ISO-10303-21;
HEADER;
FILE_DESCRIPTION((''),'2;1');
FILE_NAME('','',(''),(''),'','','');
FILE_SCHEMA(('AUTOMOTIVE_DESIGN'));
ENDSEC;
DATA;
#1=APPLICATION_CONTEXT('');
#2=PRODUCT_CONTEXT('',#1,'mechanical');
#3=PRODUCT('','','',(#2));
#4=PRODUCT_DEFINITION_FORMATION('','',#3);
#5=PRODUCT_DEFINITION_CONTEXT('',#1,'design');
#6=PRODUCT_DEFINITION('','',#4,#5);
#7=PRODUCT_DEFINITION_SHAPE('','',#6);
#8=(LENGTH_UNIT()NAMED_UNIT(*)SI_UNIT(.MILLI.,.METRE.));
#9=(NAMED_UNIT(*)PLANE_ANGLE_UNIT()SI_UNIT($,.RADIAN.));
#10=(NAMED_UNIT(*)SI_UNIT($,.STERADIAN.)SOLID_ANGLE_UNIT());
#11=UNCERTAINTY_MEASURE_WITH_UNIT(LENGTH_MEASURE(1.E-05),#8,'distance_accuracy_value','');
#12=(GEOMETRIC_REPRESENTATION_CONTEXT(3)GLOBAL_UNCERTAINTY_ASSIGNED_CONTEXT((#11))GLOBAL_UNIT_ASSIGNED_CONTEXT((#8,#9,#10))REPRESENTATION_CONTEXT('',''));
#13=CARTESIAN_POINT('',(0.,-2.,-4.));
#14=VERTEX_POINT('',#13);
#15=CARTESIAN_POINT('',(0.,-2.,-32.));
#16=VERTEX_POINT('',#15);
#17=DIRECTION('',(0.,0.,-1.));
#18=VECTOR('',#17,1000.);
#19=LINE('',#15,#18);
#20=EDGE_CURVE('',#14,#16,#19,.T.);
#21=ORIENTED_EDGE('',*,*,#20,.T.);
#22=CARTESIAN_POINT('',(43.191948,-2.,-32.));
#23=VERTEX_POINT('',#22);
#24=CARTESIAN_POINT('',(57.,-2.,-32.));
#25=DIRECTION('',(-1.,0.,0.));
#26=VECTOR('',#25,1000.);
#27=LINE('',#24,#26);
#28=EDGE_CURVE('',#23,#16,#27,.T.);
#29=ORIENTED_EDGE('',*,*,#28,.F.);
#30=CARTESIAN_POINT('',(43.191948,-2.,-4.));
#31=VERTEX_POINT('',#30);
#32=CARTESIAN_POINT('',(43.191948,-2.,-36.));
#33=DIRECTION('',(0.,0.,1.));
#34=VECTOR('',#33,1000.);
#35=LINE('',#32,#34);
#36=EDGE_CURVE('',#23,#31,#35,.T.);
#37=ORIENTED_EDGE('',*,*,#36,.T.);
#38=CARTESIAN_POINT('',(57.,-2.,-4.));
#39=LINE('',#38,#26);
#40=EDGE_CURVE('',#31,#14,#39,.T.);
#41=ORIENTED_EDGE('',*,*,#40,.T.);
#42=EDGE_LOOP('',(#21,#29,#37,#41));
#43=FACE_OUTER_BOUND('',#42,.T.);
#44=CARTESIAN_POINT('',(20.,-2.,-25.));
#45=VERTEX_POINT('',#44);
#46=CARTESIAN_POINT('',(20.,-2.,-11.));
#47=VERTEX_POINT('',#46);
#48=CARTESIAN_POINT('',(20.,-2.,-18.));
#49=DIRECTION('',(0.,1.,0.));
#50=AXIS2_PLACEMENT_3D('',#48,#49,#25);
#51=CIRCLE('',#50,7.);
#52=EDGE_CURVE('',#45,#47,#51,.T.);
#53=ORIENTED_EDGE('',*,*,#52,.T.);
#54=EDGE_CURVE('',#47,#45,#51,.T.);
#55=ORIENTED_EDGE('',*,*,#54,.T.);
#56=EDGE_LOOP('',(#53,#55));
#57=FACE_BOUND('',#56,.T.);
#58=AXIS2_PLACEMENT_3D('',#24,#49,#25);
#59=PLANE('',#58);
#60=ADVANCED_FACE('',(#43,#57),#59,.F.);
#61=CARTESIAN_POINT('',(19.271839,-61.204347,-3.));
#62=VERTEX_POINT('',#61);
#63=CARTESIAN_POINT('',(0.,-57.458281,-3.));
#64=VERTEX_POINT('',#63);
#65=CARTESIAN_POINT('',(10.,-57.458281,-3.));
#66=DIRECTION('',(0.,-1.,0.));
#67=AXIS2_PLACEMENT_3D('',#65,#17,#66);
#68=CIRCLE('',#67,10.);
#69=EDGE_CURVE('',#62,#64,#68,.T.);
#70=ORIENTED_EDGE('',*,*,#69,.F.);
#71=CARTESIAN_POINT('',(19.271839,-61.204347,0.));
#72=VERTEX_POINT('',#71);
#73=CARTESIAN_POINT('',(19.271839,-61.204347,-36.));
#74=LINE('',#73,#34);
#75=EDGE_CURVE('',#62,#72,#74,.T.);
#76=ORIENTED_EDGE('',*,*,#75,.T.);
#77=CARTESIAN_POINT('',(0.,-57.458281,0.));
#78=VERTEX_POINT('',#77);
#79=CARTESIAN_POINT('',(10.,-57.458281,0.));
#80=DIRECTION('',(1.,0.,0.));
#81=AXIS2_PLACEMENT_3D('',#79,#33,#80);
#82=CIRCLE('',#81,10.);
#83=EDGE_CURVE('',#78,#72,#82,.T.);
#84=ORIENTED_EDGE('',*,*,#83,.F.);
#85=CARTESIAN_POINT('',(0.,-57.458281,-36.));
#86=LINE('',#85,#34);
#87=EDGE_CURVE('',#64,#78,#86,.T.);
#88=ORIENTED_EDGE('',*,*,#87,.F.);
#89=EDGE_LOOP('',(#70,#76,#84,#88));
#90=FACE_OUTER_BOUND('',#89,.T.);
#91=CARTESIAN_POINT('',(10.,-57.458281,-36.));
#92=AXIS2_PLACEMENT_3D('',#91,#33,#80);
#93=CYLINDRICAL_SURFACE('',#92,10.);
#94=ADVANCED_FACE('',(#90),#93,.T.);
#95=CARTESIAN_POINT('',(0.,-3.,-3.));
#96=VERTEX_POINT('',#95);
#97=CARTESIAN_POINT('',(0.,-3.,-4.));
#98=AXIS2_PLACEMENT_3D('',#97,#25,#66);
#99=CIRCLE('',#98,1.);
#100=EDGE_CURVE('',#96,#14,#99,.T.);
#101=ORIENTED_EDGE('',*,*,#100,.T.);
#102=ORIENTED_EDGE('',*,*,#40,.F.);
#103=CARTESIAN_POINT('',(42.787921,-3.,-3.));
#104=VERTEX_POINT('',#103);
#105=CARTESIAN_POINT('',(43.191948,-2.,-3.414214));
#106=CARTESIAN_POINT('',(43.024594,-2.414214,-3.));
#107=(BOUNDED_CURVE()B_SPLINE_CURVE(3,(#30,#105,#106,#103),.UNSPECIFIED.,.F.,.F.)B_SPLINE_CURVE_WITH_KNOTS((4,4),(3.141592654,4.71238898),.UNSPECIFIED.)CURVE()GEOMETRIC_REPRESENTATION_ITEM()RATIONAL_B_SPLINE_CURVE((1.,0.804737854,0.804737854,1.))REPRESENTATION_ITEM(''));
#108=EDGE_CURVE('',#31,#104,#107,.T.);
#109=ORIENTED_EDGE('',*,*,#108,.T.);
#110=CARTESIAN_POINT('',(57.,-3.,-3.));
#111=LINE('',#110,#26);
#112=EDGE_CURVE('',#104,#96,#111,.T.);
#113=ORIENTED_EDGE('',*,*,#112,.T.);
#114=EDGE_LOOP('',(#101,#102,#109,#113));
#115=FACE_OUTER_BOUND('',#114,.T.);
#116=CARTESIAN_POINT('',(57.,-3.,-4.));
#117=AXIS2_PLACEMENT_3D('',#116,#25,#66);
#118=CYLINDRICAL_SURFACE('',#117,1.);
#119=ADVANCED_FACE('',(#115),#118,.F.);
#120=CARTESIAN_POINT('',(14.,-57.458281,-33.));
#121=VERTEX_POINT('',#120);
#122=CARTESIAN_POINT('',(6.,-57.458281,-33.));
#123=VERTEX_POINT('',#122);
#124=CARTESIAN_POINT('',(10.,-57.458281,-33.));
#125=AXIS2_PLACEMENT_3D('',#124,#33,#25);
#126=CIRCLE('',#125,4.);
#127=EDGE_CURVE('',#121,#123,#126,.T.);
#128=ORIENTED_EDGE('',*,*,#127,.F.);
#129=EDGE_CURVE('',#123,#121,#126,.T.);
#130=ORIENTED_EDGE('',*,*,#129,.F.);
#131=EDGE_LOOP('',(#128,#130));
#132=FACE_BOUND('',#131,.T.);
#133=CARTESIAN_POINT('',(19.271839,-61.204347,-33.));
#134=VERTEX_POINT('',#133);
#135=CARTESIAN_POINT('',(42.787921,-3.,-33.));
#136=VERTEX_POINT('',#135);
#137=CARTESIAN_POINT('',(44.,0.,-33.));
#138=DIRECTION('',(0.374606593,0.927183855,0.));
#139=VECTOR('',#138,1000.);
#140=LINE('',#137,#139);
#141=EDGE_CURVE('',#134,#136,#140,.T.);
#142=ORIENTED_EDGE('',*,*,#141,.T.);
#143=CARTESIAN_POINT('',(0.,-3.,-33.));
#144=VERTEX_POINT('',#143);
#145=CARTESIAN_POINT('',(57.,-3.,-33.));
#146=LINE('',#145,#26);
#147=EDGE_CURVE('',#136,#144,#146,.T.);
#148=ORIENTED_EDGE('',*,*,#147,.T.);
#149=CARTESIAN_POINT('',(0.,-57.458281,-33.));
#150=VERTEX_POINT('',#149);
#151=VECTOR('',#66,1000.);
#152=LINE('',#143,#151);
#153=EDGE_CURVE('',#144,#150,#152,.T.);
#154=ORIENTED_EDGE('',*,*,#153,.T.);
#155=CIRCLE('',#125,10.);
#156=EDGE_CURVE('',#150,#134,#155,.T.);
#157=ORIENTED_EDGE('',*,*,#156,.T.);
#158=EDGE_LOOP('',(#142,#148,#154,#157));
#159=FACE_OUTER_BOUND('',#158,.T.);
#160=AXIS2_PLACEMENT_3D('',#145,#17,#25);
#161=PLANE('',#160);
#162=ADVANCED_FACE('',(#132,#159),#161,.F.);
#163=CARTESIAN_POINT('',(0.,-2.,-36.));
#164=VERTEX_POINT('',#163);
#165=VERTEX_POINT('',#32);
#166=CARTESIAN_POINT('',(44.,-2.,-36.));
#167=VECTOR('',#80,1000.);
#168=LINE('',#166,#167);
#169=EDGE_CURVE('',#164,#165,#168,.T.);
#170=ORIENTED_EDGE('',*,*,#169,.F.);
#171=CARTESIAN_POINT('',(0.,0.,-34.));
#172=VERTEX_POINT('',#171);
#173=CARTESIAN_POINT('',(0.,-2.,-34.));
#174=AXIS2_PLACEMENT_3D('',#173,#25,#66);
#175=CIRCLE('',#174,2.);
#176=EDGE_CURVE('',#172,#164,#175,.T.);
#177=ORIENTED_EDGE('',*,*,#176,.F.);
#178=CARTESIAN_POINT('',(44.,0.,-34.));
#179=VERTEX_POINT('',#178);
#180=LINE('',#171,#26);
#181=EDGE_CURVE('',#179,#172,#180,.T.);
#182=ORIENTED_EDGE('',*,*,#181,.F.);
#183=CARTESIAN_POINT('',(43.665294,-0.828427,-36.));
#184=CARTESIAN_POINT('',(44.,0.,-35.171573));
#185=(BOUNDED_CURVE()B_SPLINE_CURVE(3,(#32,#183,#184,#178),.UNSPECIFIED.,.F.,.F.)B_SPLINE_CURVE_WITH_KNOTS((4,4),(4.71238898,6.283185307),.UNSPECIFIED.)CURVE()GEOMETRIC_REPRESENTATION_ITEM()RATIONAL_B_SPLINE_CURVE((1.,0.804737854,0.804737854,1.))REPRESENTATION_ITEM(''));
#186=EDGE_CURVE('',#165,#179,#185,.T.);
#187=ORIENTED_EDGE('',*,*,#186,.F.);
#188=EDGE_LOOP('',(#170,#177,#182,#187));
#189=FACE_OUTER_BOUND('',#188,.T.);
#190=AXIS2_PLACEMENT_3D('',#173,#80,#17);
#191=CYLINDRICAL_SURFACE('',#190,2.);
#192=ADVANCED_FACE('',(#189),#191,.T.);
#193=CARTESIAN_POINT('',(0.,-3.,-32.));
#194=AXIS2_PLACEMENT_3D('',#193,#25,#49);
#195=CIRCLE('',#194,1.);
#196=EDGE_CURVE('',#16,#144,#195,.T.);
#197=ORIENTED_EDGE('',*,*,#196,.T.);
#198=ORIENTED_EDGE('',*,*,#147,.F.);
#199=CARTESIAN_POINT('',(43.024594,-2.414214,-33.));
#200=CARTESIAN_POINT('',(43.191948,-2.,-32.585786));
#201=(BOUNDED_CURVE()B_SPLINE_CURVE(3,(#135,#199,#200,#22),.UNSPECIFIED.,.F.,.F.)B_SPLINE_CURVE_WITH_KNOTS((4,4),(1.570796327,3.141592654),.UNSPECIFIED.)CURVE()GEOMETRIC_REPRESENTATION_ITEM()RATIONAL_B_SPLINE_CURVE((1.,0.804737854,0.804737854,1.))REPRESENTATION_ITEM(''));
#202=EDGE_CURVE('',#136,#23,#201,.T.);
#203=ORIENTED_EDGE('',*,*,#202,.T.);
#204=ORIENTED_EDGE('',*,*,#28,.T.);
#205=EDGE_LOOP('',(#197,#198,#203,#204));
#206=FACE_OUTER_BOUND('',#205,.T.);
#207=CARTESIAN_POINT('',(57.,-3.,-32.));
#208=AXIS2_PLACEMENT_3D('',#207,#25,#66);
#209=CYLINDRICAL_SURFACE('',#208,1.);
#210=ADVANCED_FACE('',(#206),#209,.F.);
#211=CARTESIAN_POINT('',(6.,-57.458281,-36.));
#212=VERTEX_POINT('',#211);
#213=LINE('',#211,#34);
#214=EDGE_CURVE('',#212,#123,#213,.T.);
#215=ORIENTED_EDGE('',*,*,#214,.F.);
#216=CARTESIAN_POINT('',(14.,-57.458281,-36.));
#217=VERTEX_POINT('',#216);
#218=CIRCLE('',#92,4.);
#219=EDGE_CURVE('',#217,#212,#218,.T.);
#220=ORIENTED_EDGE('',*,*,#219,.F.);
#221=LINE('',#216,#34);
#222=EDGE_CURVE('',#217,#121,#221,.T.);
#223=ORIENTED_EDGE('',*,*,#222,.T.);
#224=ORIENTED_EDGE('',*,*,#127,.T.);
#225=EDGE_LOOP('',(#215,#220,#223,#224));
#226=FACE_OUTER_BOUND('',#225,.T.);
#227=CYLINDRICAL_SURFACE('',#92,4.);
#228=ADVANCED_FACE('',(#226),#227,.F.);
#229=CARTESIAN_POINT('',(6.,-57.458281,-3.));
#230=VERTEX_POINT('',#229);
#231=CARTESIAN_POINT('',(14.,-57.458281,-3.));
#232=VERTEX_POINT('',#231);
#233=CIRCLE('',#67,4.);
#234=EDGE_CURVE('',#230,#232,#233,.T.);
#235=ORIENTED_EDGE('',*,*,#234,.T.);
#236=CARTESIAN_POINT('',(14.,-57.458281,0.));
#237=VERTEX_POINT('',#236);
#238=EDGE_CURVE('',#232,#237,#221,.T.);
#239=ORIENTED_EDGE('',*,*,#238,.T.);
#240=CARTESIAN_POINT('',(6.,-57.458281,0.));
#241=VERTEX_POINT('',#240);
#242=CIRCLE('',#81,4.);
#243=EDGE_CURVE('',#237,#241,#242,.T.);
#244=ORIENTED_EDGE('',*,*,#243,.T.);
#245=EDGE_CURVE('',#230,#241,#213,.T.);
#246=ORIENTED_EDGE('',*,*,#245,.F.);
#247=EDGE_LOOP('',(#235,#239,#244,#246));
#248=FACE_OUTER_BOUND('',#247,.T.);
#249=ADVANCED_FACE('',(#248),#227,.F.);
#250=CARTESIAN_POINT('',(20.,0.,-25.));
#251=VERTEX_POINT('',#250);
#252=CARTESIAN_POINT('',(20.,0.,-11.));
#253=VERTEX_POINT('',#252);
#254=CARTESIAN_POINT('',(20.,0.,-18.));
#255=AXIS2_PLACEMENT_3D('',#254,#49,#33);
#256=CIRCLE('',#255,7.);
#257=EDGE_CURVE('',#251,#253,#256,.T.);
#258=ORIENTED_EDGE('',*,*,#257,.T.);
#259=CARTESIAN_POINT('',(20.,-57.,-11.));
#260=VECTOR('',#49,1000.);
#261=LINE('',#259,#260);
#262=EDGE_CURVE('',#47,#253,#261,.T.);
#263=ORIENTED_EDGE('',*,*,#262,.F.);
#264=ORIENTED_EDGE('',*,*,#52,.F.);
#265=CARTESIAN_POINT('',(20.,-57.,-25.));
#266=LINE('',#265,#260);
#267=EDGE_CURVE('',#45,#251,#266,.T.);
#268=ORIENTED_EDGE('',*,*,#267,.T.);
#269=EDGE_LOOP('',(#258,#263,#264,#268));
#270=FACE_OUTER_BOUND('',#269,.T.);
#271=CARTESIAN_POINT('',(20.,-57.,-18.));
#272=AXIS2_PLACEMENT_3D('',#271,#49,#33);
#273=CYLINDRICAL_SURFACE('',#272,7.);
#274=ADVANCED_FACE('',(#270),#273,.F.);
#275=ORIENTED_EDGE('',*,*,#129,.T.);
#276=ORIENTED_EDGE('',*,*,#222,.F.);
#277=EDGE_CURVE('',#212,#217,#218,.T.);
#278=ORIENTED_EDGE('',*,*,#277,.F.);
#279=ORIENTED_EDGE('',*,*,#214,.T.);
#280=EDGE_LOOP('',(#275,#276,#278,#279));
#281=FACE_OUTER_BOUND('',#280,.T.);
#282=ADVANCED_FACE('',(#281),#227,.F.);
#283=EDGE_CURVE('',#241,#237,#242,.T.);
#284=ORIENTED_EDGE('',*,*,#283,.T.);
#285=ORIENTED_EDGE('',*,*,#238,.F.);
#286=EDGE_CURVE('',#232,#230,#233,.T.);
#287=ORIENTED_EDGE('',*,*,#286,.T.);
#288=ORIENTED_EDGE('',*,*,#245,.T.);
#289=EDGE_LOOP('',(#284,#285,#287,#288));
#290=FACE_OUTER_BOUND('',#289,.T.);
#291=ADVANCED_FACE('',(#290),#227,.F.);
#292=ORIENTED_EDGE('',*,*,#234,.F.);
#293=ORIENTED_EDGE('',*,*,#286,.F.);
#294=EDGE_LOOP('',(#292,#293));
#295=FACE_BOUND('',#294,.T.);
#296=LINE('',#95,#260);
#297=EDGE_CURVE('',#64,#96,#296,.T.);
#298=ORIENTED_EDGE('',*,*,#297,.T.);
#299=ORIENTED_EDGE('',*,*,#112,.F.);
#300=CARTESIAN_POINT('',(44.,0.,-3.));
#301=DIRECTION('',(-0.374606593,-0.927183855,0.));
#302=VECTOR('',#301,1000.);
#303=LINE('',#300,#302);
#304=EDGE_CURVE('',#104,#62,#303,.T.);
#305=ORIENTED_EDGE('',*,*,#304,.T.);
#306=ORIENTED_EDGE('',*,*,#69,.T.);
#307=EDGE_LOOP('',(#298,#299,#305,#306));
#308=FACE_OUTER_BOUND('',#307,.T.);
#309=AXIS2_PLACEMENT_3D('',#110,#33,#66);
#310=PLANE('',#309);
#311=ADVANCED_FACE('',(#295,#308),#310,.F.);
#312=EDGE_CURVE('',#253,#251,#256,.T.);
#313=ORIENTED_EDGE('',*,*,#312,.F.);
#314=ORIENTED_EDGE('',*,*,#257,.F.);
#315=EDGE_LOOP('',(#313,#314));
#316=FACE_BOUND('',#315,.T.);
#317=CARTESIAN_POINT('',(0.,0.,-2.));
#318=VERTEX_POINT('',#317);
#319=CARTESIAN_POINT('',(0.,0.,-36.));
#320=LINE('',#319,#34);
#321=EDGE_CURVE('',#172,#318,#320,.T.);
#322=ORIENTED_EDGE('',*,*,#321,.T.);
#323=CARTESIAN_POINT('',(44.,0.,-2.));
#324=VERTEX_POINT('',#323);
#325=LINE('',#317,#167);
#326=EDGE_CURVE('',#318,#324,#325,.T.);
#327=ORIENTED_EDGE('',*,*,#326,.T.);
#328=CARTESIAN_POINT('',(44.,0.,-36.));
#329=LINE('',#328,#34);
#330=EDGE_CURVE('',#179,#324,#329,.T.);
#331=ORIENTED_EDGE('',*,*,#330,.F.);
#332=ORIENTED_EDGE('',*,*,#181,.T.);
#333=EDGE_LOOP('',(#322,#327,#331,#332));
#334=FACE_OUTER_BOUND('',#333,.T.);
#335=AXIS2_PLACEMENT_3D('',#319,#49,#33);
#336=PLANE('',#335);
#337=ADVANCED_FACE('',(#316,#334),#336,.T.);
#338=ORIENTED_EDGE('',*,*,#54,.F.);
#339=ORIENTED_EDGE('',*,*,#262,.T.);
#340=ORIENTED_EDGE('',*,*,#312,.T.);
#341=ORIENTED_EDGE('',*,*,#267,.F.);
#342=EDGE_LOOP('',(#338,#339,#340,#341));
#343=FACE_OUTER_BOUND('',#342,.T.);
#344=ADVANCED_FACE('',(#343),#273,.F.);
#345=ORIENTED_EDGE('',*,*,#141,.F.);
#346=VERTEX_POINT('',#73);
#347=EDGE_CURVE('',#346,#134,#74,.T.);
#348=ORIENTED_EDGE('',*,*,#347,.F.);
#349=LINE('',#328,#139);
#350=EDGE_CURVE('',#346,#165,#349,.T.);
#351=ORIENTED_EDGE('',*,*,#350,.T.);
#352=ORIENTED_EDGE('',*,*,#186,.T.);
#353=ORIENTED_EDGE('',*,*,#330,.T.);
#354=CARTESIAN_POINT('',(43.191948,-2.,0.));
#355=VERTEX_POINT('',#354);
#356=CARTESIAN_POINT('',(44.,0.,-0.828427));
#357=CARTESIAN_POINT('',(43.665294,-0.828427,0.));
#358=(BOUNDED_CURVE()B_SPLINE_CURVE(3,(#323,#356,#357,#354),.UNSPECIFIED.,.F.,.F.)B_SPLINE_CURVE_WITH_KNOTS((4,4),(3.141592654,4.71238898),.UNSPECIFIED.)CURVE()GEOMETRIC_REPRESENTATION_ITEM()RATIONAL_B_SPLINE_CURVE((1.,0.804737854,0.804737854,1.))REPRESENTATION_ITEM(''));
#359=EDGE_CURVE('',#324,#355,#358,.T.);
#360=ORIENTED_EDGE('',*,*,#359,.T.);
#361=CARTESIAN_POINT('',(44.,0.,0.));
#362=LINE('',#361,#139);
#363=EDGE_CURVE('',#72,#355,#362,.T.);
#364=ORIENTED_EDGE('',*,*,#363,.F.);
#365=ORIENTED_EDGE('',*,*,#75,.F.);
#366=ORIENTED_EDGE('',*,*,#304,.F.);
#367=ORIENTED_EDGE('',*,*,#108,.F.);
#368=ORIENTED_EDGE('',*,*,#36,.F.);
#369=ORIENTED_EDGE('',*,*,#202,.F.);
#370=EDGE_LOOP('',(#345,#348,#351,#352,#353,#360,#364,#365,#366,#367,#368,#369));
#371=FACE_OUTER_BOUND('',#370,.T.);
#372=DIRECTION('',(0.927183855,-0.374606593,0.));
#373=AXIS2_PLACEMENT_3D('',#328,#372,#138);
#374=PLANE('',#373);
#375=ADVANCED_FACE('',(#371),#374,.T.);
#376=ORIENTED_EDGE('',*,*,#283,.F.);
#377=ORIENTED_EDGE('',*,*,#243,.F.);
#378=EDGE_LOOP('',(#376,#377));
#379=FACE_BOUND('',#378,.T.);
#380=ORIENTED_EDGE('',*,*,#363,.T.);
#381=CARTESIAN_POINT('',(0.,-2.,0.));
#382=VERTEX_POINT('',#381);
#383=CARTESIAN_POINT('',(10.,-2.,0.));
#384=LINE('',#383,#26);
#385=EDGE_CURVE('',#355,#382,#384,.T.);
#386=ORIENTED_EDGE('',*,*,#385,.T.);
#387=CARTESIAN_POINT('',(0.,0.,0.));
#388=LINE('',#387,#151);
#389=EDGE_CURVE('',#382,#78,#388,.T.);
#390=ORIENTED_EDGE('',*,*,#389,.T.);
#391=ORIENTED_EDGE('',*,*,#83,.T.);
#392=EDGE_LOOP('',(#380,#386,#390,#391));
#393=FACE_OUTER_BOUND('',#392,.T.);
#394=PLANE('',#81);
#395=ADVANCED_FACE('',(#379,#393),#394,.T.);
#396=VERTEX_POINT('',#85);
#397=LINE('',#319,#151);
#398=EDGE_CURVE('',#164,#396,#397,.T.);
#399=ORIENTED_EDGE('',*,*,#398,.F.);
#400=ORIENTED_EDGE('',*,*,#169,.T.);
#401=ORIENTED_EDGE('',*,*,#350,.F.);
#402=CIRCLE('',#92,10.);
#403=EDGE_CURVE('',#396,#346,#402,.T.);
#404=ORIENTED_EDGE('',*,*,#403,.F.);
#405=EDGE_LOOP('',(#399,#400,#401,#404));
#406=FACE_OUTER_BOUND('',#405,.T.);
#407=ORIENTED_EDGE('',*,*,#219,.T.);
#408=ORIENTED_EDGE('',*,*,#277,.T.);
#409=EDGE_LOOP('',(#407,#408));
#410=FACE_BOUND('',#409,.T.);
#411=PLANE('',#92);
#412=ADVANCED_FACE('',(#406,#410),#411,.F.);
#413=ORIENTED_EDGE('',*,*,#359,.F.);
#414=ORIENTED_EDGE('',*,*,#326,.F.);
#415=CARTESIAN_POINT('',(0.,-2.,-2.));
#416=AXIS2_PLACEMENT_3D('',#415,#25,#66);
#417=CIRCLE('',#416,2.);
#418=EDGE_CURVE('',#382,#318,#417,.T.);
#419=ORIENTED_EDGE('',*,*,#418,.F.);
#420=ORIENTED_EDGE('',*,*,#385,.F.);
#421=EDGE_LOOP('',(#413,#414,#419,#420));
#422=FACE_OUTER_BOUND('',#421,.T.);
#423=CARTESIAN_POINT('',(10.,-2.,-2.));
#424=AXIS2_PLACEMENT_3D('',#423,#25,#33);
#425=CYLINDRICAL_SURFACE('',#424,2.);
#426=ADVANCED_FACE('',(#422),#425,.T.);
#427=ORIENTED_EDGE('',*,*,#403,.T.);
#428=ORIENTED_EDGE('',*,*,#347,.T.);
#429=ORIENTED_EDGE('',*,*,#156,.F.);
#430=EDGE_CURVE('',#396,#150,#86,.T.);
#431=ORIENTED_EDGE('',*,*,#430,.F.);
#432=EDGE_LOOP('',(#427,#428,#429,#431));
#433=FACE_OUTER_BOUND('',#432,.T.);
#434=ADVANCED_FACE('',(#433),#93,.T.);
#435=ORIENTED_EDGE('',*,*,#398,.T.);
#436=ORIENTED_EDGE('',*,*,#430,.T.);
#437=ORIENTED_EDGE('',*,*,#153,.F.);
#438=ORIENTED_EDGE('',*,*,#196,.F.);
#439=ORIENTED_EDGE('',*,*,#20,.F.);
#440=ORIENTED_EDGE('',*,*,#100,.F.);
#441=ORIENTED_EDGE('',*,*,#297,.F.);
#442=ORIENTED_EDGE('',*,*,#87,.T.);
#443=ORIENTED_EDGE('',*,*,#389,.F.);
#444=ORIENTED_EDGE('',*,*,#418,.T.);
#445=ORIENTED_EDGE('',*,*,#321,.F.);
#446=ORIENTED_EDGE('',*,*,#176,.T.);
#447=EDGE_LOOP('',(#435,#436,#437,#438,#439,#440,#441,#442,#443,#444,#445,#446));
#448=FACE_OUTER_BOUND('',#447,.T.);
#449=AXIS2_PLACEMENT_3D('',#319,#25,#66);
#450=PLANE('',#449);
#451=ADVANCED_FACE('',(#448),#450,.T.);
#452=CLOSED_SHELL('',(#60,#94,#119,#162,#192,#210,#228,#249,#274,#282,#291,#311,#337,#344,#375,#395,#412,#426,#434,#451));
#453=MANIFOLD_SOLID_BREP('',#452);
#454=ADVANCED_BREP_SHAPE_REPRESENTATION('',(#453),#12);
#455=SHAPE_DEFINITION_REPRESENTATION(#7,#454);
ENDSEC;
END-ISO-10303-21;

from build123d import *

# Parameters (mm, degrees)
SKETCH1_R           = 4
BOSS_EXTRUDE1_DEPTH = 36
CUT_EXTRUDE1_DEPTH  = 57
FILLET1_R           = 2
SKETCH3_R           = 7
CUT_EXTRUDE2_DEPTH  = 57


with BuildPart() as part:
    # Sketch1 → Boss-Extrude1 (new body)
    with BuildSketch(Plane.XY):
        with BuildLine():
            Line((0, 0), (0, -57.458281391))
            ThreePointArc((0, -57.458281391), (8.091910046, -67.274553225), (19.271838546, -61.204347325))
            Line((19.271838546, -61.204347325), (44, 0))
            Line((44, 0), (0, 0))
        make_face()
        with Locations((10, -57.458281391)):
            Circle(SKETCH1_R, mode=Mode.SUBTRACT)
    extrude(amount=-BOSS_EXTRUDE1_DEPTH)

    # Sketch2 → Cut-Extrude1 (cut)
    with BuildSketch(Plane.ZY):
        with BuildLine():
            Line((-32, -2), (-4, -2))
            ThreePointArc((-4, -2), (-3.292893219, -2.292893219), (-3, -3))
            Line((-3, -3), (-3, -57.458281391))
            Line((-3, -57.458281391), (-3, -71.28436633))
            Line((-3, -71.28436633), (-33, -71.28436633))
            Line((-33, -71.28436633), (-33, -57.458281391))
            Line((-33, -57.458281391), (-33, -3))
            ThreePointArc((-33, -3), (-32.707106781, -2.292893219), (-32, -2))
        make_face()
    extrude(amount=-CUT_EXTRUDE1_DEPTH, mode=Mode.SUBTRACT)

    # Fillet1
    fillet1_edges = [part.edges().sort_by_distance(p)[0] for p in [
        (22, 0, -36),
        (22, 0, 0),
    ]]
    fillet(fillet1_edges, radius=FILLET1_R)

    # Sketch3 → Cut-Extrude2 (cut)
    with BuildSketch(Plane(origin=(0, 0, 0), x_dir=(1, 0, 0), z_dir=(0, 1, 0))):
        with Locations(Location((20, 18, 0), (0, 0, 270))):
            Circle(SKETCH3_R)
    extrude(amount=-CUT_EXTRUDE2_DEPTH, mode=Mode.SUBTRACT)


solid = part.part
